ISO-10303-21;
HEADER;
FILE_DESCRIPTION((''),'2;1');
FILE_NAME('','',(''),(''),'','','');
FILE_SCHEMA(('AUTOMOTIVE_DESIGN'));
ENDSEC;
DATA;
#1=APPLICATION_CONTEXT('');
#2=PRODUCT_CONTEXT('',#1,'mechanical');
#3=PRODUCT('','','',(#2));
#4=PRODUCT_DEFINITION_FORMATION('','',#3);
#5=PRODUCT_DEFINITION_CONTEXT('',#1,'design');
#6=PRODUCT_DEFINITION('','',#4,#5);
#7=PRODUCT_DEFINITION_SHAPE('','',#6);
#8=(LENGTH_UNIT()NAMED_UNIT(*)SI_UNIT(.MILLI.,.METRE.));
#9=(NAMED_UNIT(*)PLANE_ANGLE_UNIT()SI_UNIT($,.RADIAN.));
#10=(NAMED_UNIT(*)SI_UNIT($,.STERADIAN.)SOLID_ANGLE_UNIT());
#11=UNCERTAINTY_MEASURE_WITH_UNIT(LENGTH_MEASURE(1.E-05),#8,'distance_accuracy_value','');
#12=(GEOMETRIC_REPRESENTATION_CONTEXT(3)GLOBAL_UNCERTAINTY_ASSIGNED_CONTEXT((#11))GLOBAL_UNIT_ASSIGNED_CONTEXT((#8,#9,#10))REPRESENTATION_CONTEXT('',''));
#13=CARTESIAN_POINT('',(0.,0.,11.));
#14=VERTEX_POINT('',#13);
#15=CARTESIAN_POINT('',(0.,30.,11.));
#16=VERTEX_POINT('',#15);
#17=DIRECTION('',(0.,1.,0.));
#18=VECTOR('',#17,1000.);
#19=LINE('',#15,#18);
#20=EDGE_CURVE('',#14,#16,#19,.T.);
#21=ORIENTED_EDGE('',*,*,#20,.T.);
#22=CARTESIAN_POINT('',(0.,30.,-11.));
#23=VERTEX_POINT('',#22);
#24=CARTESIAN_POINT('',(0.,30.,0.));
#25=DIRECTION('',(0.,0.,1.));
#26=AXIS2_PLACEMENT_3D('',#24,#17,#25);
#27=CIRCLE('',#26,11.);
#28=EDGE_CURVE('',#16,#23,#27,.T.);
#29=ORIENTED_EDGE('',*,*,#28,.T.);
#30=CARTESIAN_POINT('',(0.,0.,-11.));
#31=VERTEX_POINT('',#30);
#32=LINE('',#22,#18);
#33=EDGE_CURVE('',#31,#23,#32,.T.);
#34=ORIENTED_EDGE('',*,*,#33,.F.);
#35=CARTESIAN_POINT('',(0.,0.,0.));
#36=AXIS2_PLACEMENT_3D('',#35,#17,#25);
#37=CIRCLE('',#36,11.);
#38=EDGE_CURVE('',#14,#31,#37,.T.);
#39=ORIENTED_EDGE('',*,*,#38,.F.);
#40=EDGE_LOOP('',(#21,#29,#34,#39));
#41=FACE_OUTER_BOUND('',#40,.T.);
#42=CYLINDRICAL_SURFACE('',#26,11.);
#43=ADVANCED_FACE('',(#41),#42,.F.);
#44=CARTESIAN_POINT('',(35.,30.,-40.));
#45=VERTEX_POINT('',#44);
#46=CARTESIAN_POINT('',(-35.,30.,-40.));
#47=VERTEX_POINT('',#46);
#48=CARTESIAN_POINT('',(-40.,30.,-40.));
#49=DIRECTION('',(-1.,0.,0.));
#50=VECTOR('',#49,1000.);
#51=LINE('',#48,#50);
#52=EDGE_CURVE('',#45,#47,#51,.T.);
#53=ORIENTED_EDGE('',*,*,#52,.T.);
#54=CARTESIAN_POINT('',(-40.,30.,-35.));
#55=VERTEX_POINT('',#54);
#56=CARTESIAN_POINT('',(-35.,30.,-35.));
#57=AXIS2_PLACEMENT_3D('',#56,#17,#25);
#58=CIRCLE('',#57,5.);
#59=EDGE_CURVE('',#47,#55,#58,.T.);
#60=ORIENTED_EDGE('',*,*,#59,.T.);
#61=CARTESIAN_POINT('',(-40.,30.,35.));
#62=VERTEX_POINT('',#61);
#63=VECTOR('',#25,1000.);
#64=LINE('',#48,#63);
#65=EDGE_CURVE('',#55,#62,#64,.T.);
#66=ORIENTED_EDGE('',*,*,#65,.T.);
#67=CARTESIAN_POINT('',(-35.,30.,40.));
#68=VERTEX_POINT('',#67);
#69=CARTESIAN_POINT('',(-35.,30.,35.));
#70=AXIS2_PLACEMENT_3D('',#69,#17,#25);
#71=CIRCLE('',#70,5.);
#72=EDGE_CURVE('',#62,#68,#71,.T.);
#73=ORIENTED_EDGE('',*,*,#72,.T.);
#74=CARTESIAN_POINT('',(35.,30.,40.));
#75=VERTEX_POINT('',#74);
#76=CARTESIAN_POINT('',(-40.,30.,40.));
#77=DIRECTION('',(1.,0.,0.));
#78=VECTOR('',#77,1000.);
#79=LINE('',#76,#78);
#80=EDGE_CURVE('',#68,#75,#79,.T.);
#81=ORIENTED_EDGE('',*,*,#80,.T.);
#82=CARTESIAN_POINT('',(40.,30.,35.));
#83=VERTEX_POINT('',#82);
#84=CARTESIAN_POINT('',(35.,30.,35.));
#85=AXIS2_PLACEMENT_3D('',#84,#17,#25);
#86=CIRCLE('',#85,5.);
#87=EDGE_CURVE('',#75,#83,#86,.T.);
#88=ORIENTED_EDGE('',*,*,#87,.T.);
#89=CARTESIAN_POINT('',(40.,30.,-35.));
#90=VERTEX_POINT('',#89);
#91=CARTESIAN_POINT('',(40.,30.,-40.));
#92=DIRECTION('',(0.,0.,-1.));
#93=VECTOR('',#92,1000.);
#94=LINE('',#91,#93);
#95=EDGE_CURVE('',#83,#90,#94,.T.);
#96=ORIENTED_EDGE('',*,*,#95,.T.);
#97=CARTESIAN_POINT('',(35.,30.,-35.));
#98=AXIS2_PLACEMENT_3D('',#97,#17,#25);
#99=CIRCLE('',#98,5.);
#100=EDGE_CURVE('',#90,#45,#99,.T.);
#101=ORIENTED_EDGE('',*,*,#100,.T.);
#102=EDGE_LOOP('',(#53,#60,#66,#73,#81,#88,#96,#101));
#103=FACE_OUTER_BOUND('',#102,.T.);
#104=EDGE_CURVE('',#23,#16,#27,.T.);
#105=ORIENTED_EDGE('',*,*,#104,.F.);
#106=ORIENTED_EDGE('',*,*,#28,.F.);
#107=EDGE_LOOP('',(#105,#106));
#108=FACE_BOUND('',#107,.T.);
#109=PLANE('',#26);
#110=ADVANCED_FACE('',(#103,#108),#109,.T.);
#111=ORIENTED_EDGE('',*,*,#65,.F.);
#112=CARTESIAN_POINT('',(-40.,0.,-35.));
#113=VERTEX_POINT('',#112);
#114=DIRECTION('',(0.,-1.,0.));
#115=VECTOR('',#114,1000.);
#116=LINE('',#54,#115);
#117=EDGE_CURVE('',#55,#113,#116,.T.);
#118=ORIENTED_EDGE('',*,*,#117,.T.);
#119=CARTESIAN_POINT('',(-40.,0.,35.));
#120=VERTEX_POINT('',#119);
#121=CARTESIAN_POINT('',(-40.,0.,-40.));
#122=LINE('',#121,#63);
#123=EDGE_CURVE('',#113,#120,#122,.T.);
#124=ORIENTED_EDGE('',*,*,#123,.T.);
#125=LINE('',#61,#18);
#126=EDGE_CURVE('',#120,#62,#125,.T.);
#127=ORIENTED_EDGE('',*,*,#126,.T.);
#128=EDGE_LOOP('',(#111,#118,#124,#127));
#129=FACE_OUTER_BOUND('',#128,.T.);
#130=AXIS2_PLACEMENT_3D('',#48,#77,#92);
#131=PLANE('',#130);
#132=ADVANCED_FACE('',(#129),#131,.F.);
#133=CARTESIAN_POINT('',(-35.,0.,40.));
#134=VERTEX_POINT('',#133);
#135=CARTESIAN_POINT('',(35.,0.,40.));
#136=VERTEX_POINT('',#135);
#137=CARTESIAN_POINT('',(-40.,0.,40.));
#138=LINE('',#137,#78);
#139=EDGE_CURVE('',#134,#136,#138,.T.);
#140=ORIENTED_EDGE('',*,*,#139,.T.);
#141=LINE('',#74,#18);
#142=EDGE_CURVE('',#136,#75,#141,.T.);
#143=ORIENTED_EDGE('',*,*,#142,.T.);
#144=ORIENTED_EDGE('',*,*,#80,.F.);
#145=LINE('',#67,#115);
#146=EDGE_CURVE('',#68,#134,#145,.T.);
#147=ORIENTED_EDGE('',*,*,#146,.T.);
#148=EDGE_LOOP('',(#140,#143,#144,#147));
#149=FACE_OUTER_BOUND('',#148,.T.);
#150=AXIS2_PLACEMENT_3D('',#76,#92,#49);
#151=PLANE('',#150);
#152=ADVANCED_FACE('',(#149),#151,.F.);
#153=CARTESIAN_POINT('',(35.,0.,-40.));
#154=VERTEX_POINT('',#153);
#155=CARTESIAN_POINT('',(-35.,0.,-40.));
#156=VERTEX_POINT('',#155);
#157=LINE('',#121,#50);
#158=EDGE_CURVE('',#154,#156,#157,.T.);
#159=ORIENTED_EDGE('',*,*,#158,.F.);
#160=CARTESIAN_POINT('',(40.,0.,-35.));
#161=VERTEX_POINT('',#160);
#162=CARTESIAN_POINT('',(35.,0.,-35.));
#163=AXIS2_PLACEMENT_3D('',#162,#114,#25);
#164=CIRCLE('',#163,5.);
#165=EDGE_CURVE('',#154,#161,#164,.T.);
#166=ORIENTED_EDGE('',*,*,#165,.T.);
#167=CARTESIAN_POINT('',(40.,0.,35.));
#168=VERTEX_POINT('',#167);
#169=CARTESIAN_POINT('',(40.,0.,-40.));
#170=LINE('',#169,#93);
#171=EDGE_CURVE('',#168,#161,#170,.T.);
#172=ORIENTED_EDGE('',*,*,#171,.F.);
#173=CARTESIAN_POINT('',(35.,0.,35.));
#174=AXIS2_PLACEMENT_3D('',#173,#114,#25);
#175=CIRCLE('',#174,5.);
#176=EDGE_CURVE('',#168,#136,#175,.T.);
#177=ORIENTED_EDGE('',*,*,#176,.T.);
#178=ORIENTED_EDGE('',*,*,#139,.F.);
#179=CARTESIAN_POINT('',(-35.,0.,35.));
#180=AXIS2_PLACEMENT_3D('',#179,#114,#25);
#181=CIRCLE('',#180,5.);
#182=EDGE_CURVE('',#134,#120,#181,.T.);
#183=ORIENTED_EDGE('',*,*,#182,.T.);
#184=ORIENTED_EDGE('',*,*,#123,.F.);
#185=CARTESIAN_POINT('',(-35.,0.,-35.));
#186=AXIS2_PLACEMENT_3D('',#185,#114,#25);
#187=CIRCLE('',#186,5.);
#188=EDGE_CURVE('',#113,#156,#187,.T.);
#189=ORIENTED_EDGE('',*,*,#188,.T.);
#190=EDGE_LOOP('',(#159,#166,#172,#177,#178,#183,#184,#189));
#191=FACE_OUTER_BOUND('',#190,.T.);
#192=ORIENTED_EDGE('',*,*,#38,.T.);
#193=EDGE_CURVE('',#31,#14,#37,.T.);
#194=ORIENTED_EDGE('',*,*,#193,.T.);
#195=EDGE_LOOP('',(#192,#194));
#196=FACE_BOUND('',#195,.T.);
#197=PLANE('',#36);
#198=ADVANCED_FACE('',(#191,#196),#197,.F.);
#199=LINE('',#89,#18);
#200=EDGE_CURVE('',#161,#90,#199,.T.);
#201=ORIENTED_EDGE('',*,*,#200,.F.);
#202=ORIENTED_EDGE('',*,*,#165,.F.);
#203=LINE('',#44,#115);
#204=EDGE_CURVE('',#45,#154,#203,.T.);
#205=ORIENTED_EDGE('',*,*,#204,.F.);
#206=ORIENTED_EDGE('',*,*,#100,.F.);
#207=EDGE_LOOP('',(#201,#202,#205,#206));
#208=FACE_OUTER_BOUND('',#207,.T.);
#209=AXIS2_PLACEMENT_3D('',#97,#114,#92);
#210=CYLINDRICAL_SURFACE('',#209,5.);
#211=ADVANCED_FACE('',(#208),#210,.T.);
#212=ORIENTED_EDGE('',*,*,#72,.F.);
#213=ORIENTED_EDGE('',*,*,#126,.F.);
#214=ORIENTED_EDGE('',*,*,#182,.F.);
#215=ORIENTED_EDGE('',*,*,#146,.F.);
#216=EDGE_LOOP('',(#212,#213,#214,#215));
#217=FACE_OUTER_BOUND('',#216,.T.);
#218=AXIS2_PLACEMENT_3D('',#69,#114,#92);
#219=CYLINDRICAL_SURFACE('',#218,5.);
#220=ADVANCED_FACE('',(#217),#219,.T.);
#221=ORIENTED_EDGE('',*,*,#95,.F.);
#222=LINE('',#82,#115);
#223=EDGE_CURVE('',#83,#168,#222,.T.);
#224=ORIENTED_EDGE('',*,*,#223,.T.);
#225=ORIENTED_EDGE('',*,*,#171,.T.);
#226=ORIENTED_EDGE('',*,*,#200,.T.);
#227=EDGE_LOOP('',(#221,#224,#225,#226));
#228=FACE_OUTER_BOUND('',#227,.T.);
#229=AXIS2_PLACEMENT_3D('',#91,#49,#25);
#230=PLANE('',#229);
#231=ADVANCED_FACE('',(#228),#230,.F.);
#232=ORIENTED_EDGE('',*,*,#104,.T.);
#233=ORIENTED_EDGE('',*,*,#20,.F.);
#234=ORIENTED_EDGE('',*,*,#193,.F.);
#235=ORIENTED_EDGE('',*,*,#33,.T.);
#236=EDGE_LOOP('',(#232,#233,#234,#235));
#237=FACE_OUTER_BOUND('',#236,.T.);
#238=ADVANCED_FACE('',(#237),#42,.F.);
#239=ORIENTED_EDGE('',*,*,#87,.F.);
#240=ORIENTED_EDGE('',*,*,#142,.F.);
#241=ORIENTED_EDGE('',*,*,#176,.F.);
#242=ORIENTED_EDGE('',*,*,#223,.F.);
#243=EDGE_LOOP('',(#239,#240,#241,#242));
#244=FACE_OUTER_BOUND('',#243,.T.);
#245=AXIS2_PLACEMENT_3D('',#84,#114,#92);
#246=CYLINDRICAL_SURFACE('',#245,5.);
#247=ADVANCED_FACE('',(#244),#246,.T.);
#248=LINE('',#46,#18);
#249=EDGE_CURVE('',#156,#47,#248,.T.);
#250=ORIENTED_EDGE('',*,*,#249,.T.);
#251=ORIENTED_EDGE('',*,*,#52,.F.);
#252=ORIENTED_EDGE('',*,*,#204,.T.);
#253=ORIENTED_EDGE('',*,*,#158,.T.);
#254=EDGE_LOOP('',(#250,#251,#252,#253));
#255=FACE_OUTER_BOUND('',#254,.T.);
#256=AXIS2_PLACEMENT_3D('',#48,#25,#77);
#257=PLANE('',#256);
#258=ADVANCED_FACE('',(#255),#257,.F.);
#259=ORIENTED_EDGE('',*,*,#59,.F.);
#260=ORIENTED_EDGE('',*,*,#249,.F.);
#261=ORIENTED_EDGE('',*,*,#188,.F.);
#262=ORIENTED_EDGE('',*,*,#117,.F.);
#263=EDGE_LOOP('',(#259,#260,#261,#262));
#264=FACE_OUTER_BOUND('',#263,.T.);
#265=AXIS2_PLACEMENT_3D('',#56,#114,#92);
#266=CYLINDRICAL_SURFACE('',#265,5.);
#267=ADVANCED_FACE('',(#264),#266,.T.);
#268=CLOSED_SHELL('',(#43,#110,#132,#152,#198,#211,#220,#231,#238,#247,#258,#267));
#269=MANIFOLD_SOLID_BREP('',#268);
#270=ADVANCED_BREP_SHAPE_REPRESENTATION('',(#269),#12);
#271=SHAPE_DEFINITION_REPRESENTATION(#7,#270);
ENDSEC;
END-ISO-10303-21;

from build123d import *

# Parameters (mm, degrees)
SKETCH1_W              = 80
SKETCH1_H              = 80
BOSS_EXTRUDE1_DEPTH    = 30
FILLET1_R              = 5
M24X2_0_TAPPED_HOLE1_D = 22


with BuildPart() as part:
    # Sketch1 → Boss-Extrude1 (new body)
    with BuildSketch(Plane(origin=(0, 0, 0), x_dir=(1, 0, 0), z_dir=(0, 1, 0))):
        Rectangle(SKETCH1_W, SKETCH1_H)
    extrude(amount=BOSS_EXTRUDE1_DEPTH)

    # Fillet1
    fillet1_edges = [part.edges().sort_by_distance(p)[0] for p in [
        (40, 15, 40),
        (-40, 15, 40),
        (-40, 15, -40),
        (40, 15, -40),
    ]]
    fillet(fillet1_edges, radius=FILLET1_R)

    # M24x2.0 Tapped Hole1 (through all)
    with Locations(Plane(origin=(0, 30, 0), x_dir=(1, 0, 0), z_dir=(0, 1, 0))):
        with Locations((0, 0)):
            Hole(M24X2_0_TAPPED_HOLE1_D / 2)


solid = part.part
